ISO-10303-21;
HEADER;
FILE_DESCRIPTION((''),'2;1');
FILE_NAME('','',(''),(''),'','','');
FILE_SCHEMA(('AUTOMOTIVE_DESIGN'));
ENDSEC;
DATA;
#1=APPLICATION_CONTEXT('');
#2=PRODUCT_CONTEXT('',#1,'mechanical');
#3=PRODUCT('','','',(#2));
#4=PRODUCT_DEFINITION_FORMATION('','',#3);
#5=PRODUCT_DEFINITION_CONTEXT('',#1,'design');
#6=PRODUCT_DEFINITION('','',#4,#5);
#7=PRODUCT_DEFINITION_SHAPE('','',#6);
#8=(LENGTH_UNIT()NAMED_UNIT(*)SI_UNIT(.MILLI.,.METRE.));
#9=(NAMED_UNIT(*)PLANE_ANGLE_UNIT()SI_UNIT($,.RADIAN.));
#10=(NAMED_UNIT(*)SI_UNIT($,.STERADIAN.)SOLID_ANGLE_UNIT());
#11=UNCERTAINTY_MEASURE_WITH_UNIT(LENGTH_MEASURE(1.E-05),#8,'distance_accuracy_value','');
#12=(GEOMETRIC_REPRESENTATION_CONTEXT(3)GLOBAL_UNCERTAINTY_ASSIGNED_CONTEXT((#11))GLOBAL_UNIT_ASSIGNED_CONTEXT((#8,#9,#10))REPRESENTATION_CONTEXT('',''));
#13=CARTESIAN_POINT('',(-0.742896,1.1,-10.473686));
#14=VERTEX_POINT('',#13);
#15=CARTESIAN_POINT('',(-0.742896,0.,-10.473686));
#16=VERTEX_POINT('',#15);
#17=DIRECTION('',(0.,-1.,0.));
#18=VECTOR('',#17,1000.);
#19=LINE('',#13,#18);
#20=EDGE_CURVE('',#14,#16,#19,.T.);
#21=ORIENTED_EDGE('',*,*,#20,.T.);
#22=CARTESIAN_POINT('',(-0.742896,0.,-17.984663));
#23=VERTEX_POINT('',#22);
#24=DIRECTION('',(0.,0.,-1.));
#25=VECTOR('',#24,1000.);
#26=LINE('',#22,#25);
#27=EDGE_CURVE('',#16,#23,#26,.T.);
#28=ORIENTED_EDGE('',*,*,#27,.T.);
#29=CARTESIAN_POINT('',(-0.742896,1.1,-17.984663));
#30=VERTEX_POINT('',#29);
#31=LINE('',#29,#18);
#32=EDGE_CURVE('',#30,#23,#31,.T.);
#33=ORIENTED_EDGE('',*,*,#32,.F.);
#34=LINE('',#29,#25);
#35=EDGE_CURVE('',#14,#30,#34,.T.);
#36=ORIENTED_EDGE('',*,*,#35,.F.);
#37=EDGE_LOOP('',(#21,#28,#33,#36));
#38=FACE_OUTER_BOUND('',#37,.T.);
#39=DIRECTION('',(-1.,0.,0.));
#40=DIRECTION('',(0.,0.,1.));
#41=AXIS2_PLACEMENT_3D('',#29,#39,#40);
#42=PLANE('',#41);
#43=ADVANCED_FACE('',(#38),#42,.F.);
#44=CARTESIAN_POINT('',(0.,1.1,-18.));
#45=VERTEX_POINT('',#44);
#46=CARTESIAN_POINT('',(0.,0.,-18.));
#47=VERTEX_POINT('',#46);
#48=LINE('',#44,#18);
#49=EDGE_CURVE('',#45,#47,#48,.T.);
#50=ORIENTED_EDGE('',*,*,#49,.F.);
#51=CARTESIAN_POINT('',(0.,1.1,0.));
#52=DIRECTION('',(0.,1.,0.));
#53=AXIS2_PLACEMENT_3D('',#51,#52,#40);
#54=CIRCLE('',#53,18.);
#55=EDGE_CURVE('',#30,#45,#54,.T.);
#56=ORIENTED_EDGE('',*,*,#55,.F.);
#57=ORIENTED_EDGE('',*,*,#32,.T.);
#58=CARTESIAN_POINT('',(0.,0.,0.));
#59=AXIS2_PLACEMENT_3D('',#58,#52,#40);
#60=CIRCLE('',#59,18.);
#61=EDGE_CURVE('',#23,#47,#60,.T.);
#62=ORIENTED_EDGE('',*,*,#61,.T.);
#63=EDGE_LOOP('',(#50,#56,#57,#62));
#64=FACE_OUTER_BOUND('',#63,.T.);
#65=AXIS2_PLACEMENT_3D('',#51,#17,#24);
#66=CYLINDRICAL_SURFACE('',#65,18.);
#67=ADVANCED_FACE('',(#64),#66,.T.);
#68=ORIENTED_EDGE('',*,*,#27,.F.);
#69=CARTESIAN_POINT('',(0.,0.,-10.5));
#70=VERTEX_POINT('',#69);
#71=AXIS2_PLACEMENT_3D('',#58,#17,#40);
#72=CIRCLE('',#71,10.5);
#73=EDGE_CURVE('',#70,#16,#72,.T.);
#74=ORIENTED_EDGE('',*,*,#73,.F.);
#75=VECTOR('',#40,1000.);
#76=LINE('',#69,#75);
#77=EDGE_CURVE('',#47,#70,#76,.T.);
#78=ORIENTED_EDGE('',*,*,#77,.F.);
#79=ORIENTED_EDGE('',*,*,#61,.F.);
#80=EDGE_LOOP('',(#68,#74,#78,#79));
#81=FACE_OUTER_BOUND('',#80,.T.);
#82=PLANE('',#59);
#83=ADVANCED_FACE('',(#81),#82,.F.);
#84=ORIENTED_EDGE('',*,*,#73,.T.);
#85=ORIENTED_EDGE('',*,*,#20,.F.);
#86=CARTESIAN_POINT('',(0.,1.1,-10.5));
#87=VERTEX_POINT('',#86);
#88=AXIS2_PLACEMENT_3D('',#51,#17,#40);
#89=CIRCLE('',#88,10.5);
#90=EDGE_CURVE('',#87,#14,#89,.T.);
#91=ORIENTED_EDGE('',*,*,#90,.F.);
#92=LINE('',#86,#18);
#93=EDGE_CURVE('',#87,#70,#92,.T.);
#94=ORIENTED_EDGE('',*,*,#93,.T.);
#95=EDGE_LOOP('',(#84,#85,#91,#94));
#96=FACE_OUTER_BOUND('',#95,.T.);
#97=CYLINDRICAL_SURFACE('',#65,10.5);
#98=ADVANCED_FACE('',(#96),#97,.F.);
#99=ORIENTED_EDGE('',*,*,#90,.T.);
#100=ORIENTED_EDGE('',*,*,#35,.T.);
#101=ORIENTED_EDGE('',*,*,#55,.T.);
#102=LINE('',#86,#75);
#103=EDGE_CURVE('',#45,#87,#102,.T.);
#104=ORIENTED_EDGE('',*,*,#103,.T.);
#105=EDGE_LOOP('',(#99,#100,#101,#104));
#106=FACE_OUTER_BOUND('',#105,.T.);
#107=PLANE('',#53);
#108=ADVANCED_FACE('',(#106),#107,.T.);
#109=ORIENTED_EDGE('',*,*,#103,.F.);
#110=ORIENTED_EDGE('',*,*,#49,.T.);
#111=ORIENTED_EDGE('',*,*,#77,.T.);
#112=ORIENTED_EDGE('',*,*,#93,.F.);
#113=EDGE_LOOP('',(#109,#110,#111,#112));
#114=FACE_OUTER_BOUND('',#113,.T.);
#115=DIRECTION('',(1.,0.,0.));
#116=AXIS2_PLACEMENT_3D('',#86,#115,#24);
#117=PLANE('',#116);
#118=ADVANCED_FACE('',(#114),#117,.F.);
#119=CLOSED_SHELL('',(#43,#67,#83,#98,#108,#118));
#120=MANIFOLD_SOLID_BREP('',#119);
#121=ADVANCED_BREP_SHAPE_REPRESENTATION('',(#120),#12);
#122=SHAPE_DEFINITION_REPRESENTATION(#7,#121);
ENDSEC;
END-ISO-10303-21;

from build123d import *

# Parameters (mm, degrees)
BOSS_EXTRUDE1_DEPTH = 1.1


with BuildPart() as part:
    # Sketch1 → Boss-Extrude1 (new body)
    with BuildSketch(Plane(origin=(0, 0, 0), x_dir=(1, 0, 0), z_dir=(0, 1, 0))):
        with BuildLine():
            Line((0, 10.5), (0, 18))
            ThreePointArc((0, 18), (0.371526974, -17.996165361), (-0.742895651, 17.984663079))
            Line((-0.742895651, 17.984663079), (-0.742895651, 10.473686364))
            ThreePointArc((-0.742895651, 10.473686364), (0.371680762, -10.493419529), (0, 10.5))
        make_face()
    extrude(amount=BOSS_EXTRUDE1_DEPTH)


solid = part.part
